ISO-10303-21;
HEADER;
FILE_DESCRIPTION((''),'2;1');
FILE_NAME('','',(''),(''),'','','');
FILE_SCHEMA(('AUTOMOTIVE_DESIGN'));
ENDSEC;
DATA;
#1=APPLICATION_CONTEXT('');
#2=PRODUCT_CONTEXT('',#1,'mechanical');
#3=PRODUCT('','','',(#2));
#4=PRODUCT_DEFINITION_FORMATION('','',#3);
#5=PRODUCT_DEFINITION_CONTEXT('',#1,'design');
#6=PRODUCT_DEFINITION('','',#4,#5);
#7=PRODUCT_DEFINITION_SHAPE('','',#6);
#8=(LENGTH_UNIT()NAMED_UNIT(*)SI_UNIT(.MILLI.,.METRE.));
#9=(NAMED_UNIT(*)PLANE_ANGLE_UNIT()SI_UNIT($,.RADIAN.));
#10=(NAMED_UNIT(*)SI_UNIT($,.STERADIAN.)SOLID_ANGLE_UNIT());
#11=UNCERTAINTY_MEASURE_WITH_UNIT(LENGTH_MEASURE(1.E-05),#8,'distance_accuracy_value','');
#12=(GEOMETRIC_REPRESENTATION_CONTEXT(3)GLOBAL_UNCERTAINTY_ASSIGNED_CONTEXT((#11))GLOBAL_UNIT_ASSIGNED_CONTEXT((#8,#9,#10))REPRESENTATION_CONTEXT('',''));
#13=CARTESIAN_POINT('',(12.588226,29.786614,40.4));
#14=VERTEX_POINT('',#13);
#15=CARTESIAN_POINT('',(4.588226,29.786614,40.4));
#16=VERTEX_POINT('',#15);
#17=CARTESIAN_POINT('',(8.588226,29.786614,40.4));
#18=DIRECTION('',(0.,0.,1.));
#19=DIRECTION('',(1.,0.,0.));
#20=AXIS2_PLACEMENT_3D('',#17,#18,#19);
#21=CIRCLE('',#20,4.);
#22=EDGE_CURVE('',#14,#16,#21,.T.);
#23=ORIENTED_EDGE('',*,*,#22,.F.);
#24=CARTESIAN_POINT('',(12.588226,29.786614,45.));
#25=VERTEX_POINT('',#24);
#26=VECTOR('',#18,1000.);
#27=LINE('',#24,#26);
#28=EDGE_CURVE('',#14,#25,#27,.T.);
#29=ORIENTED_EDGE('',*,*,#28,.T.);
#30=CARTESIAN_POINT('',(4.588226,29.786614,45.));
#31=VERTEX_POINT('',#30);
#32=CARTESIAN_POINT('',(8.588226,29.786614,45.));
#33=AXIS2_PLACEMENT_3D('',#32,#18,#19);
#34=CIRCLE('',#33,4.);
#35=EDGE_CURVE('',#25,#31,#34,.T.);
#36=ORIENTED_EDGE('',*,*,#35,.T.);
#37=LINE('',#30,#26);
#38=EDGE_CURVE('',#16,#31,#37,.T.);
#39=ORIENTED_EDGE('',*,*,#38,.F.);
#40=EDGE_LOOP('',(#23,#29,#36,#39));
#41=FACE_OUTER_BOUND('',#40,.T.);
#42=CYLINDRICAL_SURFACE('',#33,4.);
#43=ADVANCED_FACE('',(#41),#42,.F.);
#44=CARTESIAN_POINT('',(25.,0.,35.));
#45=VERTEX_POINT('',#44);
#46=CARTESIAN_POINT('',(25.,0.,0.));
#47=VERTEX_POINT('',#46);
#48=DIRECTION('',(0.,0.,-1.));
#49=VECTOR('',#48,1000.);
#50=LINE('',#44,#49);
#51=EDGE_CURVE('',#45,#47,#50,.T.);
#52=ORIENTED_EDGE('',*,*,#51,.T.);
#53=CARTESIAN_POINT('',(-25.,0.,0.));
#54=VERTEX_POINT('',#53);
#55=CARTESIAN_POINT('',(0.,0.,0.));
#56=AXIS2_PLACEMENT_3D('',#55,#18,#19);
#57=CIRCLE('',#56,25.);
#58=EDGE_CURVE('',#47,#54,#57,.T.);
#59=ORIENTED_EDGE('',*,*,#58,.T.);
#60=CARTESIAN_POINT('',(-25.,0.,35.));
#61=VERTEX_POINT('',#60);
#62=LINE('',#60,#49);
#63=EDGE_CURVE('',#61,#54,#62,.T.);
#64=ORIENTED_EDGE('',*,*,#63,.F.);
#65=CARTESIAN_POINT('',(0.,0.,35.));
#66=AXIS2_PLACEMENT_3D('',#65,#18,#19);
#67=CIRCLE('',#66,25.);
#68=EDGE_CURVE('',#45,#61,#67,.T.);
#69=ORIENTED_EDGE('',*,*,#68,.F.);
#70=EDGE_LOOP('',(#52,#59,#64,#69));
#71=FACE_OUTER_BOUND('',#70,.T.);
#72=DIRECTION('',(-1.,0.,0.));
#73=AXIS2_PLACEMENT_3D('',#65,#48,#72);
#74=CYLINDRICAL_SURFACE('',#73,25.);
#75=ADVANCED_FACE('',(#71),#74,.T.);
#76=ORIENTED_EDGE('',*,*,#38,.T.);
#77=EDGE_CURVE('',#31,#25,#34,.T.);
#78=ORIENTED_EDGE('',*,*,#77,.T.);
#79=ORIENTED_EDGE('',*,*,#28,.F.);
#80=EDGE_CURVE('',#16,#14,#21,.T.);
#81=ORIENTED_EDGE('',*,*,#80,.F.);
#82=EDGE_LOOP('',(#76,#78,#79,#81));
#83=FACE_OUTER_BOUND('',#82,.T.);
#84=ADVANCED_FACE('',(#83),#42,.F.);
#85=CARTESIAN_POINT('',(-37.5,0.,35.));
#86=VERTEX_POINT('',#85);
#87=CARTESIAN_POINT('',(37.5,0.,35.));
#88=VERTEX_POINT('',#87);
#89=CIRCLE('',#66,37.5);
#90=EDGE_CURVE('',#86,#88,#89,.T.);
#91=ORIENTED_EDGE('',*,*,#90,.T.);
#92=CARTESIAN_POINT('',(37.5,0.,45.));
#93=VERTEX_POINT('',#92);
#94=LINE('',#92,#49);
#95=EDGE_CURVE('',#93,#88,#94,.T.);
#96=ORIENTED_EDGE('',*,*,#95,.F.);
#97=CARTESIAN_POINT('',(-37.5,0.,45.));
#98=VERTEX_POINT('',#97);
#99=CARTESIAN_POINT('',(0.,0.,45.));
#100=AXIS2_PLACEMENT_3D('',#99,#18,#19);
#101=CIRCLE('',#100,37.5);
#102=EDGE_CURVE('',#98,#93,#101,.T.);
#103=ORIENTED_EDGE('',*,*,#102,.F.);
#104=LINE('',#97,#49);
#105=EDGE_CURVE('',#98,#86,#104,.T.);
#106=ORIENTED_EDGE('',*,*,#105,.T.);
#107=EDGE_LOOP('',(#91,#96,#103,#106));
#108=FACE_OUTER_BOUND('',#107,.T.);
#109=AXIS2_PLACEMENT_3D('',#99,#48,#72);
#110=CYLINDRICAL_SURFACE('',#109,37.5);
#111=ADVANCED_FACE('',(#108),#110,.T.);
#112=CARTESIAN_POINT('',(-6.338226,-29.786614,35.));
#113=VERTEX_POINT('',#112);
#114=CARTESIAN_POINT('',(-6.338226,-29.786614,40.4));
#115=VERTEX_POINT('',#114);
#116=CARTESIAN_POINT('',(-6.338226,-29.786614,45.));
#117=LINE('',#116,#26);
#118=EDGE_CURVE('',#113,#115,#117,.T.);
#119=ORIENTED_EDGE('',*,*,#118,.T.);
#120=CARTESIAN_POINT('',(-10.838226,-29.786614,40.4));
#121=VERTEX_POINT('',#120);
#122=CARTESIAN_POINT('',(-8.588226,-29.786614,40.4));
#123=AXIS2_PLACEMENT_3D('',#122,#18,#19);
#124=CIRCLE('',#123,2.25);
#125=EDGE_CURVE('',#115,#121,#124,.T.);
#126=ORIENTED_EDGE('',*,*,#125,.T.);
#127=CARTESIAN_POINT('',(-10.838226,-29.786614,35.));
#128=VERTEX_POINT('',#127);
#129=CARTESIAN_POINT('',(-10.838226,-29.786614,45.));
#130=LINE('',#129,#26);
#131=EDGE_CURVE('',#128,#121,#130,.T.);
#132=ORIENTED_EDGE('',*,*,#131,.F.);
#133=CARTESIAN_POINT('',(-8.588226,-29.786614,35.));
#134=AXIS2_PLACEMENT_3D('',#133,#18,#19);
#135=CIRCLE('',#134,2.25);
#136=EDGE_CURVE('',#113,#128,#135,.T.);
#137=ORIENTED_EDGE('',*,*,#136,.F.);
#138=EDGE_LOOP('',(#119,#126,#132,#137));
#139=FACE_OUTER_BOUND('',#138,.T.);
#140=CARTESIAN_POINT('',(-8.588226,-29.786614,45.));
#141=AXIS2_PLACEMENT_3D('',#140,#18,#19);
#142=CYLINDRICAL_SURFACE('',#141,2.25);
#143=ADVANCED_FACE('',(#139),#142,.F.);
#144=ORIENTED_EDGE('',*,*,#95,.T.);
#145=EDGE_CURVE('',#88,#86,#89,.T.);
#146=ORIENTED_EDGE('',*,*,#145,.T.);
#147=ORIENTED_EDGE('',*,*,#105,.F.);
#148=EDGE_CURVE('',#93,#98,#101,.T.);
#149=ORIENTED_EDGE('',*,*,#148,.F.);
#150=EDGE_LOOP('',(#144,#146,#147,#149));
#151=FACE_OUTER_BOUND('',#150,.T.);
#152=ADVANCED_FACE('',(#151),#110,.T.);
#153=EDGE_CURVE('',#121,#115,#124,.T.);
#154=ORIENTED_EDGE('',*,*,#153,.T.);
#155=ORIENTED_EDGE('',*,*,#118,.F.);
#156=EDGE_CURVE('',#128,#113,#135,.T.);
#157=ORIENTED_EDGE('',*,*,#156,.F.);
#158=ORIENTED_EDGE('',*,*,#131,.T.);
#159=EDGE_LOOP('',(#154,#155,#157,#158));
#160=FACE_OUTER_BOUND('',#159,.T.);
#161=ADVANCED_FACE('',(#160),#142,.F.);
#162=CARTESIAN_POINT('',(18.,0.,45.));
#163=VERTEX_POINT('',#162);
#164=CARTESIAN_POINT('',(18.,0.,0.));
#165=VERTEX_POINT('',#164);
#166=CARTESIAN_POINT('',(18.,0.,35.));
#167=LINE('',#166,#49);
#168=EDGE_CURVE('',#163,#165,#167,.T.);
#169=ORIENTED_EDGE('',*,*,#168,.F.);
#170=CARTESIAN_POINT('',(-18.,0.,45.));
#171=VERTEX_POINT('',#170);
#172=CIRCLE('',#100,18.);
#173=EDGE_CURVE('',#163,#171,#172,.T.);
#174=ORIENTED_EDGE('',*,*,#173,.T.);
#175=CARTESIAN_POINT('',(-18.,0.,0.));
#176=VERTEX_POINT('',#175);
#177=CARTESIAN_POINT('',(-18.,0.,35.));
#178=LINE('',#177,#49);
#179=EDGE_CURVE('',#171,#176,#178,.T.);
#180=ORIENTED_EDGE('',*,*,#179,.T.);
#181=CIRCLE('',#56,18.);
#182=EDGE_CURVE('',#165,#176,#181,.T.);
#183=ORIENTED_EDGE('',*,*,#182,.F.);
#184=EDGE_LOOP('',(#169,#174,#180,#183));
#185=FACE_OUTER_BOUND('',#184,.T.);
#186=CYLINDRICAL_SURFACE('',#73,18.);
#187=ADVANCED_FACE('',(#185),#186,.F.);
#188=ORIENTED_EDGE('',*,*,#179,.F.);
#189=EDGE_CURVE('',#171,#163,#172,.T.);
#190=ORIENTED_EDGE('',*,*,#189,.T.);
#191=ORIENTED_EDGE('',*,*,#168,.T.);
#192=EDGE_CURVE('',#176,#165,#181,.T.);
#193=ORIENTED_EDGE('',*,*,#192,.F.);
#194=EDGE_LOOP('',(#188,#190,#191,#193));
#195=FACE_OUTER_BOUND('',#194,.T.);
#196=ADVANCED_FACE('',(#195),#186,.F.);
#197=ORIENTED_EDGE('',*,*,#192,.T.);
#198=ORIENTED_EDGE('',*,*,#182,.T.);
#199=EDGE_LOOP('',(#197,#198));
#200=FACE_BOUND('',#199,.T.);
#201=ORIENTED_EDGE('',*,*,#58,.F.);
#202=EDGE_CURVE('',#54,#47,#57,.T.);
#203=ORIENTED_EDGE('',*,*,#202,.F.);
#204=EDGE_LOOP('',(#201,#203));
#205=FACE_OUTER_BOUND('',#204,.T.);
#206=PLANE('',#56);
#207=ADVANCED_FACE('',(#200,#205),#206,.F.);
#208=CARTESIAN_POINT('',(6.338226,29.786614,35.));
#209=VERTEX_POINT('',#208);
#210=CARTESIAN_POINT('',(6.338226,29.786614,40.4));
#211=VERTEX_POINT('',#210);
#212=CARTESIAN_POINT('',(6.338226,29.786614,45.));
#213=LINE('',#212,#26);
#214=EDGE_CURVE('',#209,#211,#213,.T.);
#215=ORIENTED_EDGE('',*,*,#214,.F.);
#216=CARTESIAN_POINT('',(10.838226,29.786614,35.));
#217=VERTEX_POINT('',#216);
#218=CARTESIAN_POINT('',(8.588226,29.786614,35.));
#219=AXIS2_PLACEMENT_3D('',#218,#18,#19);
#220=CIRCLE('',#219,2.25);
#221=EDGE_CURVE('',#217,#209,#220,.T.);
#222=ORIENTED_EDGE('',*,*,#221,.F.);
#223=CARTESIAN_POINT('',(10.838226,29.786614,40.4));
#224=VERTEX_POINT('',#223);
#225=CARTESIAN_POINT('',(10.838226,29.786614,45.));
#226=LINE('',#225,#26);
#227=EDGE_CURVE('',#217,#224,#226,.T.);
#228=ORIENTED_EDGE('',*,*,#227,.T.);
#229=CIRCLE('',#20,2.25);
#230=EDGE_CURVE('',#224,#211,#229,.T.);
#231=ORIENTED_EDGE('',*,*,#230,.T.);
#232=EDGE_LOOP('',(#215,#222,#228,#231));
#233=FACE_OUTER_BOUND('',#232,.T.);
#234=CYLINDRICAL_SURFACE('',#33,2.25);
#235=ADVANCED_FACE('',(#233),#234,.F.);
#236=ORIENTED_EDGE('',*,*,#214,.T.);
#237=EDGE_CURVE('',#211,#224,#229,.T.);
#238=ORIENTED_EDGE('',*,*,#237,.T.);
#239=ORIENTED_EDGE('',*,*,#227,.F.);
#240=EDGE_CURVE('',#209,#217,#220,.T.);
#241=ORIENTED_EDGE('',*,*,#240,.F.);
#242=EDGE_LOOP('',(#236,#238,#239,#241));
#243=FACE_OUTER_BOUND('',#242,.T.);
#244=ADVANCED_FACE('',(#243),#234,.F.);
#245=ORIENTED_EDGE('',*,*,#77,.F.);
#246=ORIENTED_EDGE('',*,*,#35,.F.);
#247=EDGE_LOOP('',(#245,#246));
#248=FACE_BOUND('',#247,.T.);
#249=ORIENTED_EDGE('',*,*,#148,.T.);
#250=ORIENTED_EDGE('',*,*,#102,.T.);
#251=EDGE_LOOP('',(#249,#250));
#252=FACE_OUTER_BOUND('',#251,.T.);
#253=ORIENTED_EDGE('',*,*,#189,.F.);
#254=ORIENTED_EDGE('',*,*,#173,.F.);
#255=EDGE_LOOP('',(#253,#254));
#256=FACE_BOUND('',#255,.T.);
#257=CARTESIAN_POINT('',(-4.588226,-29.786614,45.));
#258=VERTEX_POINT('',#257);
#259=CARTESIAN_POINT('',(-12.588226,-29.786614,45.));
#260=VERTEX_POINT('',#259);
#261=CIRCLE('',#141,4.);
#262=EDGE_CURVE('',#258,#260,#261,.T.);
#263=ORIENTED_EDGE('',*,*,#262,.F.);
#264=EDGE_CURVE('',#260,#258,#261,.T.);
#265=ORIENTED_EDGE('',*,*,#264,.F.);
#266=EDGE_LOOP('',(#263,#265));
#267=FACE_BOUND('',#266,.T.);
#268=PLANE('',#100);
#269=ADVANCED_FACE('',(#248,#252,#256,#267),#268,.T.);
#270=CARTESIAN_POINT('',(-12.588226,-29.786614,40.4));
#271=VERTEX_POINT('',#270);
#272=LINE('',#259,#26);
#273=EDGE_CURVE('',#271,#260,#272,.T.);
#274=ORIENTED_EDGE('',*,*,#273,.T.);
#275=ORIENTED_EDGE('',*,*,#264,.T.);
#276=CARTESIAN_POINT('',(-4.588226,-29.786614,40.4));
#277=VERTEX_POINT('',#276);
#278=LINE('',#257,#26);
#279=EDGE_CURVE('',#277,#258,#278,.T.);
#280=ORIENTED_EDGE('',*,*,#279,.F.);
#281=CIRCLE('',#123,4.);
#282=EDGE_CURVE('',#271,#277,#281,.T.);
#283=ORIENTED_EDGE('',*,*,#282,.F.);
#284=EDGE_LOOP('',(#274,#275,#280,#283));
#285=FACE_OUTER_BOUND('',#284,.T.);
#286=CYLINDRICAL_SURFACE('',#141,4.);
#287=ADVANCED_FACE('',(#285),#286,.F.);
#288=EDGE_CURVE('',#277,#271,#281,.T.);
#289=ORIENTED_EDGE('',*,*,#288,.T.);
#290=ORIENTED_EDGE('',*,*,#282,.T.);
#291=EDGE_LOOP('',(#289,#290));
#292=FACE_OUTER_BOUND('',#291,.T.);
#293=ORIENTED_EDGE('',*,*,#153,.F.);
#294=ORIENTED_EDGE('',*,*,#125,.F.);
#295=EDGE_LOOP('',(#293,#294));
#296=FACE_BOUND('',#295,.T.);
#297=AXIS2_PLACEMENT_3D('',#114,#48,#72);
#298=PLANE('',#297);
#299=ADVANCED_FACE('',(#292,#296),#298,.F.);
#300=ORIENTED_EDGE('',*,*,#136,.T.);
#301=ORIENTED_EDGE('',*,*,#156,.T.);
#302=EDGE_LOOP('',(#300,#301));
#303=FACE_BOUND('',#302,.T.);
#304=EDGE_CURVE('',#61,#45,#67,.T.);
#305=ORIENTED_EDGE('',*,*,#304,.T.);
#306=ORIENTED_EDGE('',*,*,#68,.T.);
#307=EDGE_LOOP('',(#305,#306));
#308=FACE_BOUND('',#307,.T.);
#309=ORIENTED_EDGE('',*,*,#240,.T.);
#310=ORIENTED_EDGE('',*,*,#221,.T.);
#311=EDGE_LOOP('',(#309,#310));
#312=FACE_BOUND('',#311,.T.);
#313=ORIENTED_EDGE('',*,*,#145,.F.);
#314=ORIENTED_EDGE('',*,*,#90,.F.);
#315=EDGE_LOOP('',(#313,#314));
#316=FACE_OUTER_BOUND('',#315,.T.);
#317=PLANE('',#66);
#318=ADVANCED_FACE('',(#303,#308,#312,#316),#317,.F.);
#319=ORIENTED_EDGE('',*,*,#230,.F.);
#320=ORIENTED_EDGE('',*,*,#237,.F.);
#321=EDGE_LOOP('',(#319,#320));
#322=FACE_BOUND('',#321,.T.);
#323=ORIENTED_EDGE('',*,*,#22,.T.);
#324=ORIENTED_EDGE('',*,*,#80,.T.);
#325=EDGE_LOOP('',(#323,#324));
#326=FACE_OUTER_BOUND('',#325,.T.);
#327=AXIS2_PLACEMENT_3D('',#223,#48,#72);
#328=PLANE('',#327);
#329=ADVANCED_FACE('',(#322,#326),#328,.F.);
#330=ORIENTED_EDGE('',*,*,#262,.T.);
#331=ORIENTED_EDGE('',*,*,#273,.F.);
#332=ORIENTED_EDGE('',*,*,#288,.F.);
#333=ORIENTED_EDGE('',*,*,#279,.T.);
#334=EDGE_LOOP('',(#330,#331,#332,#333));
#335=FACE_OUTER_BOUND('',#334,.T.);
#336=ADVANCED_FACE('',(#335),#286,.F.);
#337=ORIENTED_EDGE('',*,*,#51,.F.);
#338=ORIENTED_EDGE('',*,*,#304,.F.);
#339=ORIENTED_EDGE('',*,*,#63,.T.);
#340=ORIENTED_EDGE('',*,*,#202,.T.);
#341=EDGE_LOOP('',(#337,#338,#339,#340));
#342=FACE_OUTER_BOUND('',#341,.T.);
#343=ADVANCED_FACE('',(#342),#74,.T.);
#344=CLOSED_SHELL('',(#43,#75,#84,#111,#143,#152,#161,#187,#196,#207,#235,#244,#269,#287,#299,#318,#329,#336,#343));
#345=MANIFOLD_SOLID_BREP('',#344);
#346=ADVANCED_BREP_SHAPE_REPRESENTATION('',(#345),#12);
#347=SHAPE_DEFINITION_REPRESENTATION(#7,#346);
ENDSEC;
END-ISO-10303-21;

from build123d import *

# Parameters (mm, degrees)
SKETCH1_R                                            = 25
SKETCH1_R_2                                          = 18
BOSS_EXTRUDE1_DEPTH                                  = 35
SKETCH2_R                                            = 37.5
SKETCH2_R_2                                          = 18
BOSS_EXTRUDE2_DEPTH                                  = 10
HOLE_SIZE_PER_SOCKET_HEAD_CAP_SCREW_TYPE_D           = 4.5
HOLE_SIZE_PER_SOCKET_HEAD_CAP_SCREW_TYPE_CBORE_D     = 8
HOLE_SIZE_PER_SOCKET_HEAD_CAP_SCREW_TYPE_CBORE_DEPTH = 4.6


with BuildPart() as part:
    # Sketch1 → Boss-Extrude1 (new body)
    with BuildSketch(Plane.XY):
        Circle(SKETCH1_R)
        Circle(SKETCH1_R_2, mode=Mode.SUBTRACT)
    extrude(amount=BOSS_EXTRUDE1_DEPTH)

    # Sketch2 → Boss-Extrude2 (add)
    with BuildSketch(Plane.XY.offset(35)):
        Circle(SKETCH2_R)
        Circle(SKETCH2_R_2, mode=Mode.SUBTRACT)
    extrude(amount=BOSS_EXTRUDE2_DEPTH)

    # Hole size per socket head cap screw type3 (through all)
    with Locations(Plane.XY.offset(45)):
        with Locations((-8.588225841, -29.786614056), (8.588225841, 29.786614056)):
            CounterBoreHole(HOLE_SIZE_PER_SOCKET_HEAD_CAP_SCREW_TYPE_D / 2, HOLE_SIZE_PER_SOCKET_HEAD_CAP_SCREW_TYPE_CBORE_D / 2, HOLE_SIZE_PER_SOCKET_HEAD_CAP_SCREW_TYPE_CBORE_DEPTH)


solid = part.part
